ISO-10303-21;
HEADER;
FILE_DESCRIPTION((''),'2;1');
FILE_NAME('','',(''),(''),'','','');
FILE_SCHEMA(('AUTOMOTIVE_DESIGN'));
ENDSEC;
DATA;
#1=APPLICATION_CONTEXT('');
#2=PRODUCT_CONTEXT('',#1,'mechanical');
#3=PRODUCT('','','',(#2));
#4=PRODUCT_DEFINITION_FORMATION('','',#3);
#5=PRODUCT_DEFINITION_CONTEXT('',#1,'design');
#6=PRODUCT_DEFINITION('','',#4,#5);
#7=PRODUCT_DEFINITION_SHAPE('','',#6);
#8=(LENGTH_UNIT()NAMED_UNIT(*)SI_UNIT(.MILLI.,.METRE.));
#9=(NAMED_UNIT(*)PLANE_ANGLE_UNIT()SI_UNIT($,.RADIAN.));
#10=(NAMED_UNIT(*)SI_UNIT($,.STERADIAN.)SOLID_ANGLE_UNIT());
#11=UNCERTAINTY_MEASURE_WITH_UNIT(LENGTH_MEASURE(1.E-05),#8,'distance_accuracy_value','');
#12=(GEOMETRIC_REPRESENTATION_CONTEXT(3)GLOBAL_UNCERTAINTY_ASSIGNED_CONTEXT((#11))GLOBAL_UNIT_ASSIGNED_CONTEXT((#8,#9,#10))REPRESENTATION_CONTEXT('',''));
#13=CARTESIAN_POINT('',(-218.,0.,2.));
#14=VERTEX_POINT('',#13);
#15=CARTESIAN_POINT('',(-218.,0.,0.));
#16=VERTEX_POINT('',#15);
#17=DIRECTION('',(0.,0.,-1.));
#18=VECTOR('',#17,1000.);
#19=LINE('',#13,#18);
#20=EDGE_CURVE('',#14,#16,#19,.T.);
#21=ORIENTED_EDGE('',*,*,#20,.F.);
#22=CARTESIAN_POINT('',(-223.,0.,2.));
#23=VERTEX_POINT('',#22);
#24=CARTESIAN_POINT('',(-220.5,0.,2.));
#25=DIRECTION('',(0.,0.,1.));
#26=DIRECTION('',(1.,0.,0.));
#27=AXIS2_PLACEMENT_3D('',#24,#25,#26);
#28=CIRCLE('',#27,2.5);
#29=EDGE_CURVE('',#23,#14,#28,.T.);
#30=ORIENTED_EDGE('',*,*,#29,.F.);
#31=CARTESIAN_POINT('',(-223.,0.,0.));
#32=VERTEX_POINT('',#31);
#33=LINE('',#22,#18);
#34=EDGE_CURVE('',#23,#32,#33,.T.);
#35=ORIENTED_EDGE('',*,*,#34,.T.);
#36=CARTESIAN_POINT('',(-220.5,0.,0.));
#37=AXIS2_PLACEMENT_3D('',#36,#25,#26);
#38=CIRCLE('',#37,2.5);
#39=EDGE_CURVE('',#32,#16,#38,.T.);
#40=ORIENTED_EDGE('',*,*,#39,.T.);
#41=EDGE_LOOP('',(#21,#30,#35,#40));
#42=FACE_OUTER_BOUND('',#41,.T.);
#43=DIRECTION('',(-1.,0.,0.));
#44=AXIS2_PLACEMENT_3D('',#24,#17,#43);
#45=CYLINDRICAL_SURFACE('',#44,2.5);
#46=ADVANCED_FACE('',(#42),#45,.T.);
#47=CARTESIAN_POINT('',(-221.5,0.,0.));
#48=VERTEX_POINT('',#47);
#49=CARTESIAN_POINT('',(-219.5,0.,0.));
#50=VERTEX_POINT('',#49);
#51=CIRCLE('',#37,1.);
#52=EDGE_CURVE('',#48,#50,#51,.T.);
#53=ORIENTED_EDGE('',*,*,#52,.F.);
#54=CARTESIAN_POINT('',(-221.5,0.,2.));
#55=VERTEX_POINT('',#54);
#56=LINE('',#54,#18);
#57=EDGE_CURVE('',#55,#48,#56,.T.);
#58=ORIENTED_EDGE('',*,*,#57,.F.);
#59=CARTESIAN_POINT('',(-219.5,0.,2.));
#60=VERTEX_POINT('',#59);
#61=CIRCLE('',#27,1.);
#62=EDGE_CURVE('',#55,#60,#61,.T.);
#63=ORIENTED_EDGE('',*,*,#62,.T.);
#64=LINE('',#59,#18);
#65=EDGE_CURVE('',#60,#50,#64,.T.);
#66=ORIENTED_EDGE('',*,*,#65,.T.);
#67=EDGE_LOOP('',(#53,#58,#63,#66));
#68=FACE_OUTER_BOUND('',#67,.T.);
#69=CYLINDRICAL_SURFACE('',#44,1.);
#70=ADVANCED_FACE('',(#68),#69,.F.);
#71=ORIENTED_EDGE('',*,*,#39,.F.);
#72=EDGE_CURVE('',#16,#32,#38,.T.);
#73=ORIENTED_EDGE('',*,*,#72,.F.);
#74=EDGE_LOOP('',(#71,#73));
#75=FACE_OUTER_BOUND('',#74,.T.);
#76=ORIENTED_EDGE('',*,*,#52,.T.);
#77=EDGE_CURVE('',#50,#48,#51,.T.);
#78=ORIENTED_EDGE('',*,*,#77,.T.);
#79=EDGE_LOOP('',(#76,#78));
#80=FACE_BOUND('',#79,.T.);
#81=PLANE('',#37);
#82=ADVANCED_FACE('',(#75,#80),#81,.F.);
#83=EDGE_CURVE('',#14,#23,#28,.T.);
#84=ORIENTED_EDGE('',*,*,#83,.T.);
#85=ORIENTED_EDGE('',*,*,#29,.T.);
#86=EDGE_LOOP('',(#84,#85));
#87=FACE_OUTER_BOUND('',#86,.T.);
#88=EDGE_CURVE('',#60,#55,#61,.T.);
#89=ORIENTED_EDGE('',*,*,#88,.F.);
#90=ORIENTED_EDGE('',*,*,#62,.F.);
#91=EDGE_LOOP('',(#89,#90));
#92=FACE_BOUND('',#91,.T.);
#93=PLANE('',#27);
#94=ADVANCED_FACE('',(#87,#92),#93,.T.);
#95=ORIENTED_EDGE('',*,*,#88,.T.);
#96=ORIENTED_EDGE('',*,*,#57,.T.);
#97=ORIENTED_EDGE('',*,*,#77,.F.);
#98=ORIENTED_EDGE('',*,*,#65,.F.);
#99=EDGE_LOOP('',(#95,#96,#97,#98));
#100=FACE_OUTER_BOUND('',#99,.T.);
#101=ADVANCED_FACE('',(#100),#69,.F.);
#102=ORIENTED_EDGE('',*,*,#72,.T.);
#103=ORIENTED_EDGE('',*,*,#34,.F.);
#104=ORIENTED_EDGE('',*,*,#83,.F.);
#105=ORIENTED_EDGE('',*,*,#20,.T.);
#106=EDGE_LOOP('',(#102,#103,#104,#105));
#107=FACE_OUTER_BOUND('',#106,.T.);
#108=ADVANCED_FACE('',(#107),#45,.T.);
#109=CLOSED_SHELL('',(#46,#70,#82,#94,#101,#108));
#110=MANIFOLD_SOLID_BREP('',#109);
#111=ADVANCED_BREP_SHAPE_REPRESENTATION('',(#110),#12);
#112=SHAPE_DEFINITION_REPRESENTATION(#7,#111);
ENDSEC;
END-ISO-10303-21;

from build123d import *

# Parameters (mm, degrees)
SKETCH1_R           = 2.5
SKETCH1_R_2         = 1
BOSS_EXTRUDE1_DEPTH = 2


with BuildPart() as part:
    # Sketch1 → Boss-Extrude1 (new body)
    with BuildSketch(Plane.XY):
        with Locations((-220.5, 0)):
            Circle(SKETCH1_R)
        with Locations((-220.5, 0)):
            Circle(SKETCH1_R_2, mode=Mode.SUBTRACT)
    extrude(amount=BOSS_EXTRUDE1_DEPTH)


solid = part.part
